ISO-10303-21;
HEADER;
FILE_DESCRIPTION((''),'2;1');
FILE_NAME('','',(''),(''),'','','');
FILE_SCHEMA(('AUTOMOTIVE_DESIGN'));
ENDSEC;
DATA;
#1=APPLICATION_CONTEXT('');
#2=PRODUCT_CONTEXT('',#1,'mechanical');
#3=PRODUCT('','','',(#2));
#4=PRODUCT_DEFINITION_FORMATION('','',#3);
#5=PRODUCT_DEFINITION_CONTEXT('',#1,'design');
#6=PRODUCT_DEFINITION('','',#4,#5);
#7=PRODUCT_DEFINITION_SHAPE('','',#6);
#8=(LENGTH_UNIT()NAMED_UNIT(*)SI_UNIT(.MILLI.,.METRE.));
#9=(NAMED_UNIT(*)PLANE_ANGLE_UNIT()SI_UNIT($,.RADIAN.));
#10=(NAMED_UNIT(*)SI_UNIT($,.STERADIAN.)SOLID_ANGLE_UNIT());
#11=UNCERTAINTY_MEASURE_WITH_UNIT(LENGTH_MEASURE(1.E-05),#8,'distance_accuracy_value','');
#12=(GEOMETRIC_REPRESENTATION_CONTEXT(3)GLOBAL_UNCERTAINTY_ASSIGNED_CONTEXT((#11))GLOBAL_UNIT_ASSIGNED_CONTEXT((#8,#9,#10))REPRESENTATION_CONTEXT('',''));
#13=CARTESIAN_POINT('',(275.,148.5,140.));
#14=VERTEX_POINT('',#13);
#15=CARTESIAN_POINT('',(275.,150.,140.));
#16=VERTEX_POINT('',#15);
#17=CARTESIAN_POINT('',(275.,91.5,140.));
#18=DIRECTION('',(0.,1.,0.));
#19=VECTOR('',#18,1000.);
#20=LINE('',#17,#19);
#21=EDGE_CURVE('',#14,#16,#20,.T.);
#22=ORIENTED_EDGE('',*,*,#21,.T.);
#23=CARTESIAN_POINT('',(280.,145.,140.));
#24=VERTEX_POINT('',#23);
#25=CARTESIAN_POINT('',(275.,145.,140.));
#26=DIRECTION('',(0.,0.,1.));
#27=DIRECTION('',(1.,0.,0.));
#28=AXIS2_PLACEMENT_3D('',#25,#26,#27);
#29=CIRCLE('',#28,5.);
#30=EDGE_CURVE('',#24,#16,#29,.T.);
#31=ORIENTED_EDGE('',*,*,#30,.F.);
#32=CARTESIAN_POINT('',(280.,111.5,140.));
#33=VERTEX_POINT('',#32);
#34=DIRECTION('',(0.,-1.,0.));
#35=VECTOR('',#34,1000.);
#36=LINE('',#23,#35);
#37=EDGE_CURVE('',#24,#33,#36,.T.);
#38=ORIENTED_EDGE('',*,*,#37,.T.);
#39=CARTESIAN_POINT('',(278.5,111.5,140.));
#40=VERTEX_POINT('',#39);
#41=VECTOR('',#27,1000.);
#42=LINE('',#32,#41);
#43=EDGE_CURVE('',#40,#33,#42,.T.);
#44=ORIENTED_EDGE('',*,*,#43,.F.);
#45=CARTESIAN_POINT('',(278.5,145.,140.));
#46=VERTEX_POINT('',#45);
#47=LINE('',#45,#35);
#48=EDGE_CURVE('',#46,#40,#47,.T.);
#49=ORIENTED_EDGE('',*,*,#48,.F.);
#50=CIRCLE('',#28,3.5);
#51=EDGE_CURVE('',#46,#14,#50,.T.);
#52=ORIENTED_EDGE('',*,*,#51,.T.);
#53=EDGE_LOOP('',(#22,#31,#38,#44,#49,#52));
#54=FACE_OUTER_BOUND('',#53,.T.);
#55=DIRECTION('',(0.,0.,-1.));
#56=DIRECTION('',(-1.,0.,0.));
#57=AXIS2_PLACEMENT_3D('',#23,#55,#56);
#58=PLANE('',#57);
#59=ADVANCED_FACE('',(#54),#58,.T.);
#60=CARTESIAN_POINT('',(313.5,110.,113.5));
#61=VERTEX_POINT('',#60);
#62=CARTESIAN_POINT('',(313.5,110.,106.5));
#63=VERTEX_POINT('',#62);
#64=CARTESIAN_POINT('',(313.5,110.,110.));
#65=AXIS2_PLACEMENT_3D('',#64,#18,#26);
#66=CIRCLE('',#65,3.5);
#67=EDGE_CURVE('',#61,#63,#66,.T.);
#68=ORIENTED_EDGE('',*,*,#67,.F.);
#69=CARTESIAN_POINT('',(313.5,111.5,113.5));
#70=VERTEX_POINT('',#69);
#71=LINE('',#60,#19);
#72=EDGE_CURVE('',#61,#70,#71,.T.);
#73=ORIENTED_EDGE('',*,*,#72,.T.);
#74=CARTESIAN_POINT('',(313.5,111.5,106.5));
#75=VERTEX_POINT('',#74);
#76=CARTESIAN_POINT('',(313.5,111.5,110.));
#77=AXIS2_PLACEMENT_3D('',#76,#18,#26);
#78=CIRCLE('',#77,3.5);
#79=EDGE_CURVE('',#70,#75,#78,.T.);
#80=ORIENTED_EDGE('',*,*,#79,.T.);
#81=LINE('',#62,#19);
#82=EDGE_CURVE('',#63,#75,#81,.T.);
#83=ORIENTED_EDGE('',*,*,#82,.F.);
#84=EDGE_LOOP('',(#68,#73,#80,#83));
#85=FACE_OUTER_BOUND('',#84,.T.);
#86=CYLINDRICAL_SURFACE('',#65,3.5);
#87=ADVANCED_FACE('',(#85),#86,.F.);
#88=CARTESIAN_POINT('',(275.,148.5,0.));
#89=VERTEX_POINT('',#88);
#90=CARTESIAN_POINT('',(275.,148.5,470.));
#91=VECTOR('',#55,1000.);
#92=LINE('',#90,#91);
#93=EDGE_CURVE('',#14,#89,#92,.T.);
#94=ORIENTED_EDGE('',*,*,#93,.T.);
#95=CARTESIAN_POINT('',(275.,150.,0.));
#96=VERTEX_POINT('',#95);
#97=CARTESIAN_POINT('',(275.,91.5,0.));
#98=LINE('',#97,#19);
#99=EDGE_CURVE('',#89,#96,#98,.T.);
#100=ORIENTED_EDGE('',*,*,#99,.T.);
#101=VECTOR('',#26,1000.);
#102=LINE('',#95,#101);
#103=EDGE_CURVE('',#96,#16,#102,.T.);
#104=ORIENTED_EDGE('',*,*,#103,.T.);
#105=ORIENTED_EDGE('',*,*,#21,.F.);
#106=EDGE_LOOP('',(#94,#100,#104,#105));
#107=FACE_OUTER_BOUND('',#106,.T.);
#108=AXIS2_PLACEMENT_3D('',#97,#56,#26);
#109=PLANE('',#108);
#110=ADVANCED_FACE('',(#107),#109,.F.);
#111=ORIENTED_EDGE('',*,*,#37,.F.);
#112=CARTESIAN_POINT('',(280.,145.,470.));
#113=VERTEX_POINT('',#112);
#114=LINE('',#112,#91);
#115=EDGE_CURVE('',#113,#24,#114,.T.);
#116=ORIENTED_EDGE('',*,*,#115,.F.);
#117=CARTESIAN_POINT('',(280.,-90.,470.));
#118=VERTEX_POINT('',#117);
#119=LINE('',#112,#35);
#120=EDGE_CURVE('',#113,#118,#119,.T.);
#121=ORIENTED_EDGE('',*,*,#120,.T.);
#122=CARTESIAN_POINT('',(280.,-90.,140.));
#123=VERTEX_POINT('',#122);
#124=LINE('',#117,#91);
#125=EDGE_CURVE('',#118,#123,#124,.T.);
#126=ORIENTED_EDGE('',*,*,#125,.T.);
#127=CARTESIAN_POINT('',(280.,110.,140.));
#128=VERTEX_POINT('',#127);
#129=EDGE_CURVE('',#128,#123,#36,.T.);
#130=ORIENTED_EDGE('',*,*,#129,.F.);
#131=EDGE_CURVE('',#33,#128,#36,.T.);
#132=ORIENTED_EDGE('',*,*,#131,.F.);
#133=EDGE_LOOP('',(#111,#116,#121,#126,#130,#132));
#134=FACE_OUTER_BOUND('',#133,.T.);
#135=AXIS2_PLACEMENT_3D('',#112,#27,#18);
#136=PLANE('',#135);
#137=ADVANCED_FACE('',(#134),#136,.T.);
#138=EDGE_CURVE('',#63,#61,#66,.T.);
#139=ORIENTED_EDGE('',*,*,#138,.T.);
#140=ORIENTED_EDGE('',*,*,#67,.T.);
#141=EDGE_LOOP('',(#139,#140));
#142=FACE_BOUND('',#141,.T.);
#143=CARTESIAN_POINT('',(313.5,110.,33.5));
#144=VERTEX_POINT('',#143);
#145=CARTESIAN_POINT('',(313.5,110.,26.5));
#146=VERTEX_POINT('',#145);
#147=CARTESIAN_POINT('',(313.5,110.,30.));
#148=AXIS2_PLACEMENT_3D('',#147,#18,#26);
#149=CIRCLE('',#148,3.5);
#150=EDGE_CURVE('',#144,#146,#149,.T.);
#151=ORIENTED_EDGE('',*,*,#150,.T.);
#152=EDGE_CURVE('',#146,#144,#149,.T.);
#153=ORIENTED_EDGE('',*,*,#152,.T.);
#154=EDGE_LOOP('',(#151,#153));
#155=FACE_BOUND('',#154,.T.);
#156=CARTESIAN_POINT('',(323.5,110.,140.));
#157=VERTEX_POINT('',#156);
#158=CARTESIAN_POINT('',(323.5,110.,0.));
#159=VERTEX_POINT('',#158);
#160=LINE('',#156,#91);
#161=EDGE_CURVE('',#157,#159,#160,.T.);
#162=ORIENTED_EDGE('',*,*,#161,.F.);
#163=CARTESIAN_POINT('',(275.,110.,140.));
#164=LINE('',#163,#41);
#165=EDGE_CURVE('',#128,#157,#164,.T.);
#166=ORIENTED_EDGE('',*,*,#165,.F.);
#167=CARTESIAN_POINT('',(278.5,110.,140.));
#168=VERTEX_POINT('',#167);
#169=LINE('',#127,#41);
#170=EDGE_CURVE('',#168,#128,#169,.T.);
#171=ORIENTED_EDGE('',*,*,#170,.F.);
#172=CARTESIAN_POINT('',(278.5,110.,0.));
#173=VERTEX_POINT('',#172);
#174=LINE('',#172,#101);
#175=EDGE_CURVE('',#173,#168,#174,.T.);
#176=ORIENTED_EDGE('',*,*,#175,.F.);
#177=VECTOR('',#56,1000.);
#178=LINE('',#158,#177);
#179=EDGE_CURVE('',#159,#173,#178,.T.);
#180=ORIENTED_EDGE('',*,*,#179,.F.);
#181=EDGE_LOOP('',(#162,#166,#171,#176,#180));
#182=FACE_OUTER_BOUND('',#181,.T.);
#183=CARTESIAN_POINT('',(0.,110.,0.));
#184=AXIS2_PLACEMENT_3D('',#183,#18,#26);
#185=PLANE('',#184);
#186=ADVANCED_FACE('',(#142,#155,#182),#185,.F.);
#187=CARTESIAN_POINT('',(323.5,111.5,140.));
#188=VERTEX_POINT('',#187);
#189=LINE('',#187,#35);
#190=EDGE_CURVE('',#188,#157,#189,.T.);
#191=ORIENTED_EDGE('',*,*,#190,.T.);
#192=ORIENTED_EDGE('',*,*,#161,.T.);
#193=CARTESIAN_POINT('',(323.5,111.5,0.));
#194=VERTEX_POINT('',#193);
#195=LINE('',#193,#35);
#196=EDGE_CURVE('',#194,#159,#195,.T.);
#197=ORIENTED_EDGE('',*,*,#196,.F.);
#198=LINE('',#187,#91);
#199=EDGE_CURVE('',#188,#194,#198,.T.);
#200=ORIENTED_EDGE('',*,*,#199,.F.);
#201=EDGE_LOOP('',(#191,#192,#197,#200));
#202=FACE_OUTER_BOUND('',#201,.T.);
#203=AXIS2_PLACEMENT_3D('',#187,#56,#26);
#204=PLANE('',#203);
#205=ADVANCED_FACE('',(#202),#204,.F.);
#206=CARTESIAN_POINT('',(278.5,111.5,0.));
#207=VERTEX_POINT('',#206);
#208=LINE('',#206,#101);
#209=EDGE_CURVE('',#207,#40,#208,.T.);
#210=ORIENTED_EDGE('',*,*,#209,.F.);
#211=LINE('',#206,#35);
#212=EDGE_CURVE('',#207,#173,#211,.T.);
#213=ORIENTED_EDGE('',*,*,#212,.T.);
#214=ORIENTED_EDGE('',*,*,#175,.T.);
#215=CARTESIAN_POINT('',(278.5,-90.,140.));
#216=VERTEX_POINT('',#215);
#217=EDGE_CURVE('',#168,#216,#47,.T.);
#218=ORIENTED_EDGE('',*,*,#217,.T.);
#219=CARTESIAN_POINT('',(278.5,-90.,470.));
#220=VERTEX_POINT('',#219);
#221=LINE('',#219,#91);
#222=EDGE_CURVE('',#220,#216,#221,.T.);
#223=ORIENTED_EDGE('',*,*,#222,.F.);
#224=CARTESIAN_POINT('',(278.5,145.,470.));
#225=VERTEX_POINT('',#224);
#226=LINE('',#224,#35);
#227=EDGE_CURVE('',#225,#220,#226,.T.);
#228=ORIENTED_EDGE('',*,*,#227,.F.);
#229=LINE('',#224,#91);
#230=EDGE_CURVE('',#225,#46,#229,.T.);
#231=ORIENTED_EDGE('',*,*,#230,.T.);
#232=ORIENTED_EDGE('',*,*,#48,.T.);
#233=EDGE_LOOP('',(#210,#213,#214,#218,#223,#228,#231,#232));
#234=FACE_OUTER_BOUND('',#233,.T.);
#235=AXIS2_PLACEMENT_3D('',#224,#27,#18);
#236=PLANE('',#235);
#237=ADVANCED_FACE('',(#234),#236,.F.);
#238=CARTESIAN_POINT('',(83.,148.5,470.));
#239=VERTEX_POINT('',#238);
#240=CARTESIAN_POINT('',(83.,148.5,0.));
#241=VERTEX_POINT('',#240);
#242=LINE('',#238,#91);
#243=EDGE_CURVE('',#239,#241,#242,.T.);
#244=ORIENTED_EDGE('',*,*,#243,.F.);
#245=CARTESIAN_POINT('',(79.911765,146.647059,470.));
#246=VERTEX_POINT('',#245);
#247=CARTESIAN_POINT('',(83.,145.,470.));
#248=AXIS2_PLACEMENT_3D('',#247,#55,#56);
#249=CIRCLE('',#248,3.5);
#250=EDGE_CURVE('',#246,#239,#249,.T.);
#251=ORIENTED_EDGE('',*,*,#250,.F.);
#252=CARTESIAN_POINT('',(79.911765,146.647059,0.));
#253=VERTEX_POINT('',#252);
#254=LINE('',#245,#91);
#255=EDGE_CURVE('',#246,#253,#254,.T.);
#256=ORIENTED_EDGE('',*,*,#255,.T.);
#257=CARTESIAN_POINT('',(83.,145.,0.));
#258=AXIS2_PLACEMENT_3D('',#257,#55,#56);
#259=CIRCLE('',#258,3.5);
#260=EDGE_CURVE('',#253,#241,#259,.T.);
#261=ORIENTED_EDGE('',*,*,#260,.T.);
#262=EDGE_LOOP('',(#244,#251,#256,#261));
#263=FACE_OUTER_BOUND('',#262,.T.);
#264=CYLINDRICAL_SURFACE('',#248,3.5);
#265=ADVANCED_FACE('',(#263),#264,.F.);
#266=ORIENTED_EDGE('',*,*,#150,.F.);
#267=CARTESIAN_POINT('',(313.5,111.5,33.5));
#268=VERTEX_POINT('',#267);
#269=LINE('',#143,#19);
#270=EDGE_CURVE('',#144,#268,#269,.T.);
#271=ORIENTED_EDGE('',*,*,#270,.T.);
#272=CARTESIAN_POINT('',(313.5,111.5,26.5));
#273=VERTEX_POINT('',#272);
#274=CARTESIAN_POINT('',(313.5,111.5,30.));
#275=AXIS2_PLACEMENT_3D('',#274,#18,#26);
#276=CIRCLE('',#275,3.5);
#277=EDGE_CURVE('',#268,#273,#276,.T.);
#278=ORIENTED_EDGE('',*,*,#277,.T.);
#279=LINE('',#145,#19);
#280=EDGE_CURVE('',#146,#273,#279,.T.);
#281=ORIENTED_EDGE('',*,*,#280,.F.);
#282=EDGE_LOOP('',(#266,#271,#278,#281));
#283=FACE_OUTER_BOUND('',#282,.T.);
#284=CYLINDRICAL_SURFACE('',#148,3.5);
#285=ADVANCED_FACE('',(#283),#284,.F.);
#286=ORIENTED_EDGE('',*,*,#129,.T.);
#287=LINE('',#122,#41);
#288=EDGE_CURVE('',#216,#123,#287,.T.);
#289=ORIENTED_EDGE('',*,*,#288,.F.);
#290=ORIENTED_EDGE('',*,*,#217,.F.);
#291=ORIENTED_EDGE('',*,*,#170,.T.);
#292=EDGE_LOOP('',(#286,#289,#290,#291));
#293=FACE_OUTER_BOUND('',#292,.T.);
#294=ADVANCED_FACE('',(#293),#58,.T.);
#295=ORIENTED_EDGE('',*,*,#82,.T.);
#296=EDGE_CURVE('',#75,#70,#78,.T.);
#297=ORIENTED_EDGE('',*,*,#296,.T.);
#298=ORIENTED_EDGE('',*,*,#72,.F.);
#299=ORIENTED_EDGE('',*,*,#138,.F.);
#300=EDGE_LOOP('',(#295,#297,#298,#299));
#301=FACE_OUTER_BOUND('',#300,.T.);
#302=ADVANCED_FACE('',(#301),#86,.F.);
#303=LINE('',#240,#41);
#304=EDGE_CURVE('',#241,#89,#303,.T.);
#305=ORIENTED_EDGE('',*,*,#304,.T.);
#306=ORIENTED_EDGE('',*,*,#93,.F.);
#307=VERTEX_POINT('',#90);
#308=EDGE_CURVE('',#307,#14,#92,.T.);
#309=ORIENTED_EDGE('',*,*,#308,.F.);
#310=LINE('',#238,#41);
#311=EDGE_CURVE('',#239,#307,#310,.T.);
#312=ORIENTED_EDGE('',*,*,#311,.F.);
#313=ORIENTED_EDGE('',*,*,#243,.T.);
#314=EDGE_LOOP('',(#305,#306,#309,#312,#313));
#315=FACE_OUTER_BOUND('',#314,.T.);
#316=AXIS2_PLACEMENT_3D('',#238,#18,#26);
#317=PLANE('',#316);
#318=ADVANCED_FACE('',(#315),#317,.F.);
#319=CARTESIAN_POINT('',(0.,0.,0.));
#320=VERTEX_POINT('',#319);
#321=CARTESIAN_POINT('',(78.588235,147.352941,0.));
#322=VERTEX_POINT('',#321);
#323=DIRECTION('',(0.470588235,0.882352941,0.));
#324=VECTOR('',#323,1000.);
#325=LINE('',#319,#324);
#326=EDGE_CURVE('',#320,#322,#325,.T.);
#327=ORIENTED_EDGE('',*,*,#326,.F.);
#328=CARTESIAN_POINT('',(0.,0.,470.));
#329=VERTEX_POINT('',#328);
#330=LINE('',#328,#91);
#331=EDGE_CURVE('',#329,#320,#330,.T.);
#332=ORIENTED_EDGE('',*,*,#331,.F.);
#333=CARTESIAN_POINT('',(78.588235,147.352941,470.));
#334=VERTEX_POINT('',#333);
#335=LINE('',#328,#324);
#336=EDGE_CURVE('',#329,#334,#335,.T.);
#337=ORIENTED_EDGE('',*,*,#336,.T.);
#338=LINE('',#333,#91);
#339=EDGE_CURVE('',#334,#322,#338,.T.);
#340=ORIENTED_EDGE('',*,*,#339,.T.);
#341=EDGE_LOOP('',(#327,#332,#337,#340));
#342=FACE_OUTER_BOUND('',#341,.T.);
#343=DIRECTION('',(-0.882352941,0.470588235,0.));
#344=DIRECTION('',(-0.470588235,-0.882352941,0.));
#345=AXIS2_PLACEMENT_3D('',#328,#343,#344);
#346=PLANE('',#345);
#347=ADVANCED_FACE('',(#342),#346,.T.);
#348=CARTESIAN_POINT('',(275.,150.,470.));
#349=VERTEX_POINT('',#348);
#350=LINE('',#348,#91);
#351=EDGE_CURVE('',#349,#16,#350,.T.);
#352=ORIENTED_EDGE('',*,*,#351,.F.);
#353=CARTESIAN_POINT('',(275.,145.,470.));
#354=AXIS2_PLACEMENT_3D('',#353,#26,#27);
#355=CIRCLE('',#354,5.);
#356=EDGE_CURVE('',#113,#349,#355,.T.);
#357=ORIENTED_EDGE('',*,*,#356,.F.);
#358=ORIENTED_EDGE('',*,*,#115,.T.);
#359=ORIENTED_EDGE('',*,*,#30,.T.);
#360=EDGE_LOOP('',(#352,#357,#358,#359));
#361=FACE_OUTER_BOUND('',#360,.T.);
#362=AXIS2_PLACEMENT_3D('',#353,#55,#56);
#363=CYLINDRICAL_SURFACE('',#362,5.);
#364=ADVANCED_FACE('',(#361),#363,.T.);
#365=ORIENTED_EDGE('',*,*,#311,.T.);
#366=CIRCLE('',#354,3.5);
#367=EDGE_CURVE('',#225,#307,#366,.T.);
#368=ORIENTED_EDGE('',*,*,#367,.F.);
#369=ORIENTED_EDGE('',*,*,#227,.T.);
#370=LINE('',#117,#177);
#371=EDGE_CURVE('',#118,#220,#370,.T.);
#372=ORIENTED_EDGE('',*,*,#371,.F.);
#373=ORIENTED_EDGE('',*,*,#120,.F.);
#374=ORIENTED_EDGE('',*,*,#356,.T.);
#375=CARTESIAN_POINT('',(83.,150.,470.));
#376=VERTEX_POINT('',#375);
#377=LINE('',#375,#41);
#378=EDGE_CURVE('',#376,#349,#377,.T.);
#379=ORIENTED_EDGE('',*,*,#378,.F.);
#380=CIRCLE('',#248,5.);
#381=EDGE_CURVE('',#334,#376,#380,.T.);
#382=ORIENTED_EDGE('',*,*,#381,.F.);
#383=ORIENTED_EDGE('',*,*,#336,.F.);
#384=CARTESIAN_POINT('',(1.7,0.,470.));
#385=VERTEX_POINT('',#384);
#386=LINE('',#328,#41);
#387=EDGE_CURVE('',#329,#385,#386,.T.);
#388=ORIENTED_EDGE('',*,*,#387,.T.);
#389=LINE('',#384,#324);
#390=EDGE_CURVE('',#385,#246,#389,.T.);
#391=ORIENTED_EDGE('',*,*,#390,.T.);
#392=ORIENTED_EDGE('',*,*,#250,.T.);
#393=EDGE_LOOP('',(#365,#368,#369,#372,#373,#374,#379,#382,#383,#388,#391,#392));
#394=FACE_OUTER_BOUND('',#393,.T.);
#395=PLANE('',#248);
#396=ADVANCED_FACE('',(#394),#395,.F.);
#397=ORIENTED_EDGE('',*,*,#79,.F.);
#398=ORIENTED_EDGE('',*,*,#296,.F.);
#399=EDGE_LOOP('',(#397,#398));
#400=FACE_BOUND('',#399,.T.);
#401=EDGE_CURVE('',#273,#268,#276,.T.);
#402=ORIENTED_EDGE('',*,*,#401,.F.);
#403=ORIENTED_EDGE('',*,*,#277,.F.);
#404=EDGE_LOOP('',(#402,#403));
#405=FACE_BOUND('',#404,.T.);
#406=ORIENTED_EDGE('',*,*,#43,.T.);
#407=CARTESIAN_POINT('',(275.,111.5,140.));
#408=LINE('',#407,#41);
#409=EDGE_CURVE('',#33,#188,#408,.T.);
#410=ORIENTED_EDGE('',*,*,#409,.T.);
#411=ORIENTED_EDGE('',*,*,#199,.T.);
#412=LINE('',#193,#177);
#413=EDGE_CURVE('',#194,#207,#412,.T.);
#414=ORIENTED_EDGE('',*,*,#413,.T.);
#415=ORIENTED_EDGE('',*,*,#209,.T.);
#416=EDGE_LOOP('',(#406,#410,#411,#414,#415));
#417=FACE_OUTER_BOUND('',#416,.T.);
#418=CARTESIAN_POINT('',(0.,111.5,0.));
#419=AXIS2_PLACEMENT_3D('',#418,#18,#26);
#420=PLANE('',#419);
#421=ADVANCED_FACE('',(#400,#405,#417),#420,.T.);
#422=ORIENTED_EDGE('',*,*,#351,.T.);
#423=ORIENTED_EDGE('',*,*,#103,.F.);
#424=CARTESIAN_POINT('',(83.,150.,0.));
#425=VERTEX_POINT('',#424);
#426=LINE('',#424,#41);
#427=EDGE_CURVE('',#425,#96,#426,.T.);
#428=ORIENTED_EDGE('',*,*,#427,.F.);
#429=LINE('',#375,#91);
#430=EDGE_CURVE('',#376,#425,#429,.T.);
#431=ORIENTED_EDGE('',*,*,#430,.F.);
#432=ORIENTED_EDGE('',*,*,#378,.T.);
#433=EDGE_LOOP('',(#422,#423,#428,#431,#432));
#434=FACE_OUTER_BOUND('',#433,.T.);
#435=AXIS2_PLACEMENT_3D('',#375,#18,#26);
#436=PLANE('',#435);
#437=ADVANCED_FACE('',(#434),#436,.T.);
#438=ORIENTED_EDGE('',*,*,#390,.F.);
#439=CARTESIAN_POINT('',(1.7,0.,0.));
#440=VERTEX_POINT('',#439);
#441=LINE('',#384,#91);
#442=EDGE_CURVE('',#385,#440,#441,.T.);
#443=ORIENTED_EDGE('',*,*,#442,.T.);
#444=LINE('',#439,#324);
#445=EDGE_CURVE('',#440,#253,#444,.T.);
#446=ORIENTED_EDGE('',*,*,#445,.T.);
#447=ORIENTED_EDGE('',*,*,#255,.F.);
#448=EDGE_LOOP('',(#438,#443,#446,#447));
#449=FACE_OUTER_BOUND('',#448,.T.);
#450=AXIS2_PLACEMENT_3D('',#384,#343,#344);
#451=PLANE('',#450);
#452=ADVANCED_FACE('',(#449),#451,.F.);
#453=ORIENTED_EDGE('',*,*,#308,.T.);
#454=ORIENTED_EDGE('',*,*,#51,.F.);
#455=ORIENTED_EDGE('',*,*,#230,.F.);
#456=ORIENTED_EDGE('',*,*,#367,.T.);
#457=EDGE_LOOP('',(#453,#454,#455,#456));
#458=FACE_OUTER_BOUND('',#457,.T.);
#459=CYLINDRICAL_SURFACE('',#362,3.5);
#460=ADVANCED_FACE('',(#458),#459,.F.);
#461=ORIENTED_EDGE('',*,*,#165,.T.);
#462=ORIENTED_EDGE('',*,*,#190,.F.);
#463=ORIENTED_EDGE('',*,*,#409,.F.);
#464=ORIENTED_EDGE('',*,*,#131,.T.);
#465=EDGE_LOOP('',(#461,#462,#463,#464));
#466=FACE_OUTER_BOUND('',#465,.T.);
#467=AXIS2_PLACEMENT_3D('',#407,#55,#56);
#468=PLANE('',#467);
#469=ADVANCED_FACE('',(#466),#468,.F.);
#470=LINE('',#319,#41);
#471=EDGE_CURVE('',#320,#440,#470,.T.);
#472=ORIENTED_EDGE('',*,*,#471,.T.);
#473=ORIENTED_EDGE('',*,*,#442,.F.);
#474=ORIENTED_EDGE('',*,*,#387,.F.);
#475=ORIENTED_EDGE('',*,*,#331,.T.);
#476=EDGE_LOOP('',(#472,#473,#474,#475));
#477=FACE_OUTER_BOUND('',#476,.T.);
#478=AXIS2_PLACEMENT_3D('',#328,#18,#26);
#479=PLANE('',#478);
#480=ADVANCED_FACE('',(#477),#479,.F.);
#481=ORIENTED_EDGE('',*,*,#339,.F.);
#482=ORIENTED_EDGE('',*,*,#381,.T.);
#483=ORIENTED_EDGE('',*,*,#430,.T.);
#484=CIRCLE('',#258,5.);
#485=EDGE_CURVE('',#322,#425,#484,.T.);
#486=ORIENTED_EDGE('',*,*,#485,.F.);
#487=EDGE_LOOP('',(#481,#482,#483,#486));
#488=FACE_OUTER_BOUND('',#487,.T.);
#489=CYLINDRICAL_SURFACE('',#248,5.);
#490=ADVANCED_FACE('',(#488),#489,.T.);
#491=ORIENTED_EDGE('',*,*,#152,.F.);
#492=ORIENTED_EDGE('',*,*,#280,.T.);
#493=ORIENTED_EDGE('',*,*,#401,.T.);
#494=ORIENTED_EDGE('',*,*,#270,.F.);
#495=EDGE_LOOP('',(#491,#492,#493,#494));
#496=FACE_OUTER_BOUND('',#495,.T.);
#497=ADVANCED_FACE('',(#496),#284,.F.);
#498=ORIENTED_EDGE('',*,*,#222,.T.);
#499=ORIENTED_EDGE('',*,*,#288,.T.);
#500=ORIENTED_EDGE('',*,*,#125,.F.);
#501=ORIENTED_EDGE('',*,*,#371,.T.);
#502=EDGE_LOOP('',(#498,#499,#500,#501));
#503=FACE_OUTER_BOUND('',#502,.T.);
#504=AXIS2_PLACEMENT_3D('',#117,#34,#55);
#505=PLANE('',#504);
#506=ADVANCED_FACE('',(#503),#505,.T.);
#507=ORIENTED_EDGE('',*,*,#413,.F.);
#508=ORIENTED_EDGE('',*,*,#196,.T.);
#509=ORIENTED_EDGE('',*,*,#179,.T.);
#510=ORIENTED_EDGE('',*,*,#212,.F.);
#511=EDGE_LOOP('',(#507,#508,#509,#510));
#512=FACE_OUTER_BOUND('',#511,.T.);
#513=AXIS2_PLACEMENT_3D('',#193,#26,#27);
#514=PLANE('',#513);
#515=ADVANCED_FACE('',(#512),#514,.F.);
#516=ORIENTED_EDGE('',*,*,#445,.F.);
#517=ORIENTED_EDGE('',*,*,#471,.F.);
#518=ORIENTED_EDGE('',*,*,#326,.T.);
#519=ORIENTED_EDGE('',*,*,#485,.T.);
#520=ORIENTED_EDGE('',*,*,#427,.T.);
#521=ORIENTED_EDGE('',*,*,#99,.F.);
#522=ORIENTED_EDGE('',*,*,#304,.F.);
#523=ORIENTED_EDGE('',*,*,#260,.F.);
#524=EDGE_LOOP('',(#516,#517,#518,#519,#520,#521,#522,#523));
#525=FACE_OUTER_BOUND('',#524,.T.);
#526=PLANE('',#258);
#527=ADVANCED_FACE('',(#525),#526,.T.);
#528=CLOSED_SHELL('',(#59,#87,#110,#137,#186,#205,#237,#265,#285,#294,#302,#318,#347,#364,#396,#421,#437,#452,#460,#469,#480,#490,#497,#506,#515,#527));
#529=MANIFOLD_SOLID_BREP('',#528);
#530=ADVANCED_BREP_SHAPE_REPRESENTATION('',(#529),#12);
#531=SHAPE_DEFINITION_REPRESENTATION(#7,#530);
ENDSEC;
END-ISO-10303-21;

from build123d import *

# Parameters (mm, degrees)
BOSS_EXTRUDE1_DEPTH = 470
SKETCH2_W           = 259.384711363
SKETCH2_H           = 314.468537248
CUT_EXTRUDE3_DEPTH  = 1.5
SKETCH5_W           = 57.928223487
SKETCH5_H           = 140
CUT_EXTRUDE9_DEPTH  = 58.5
SKETCH7_W           = 48.5
SKETCH7_H           = 140
BOSS_EXTRUDE3_DEPTH = 1.5
MOVE_FACE1_BY       = 3.5
SKETCH9_R           = 3.5
CUT_EXTRUDE10_DEPTH = 1.5


with BuildPart() as part:
    # Sketch1 → Boss-Extrude1 (new body)
    with BuildSketch(Plane.XY):
        with BuildLine():
            Line((0, 0), (78.588235294, 147.352941176))
            ThreePointArc((78.588235294, 147.352941176), (80.427521223, 149.287464629), (83, 150))
            Line((83, 150), (275, 150))
            ThreePointArc((275, 150), (278.535533906, 148.535533906), (280, 145))
            Line((280, 145), (280, -90))
            Line((280, -90), (278.5, -90))
            Line((278.5, -90), (278.5, 145))
            ThreePointArc((278.5, 145), (277.474873734, 147.474873734), (275, 148.5))
            Line((275, 148.5), (83, 148.5))
            ThreePointArc((83, 148.5), (81.199264856, 148.00122524), (79.911764706, 146.647058824))
            Line((79.911764706, 146.647058824), (1.7, 0))
            Line((1.7, 0), (0, 0))
        make_face()
    extrude(amount=BOSS_EXTRUDE1_DEPTH)

    # Sketch2 → Cut-Extrude3 (cut)
    with BuildSketch(Plane.ZY.offset(-278.5)):
        with Locations((10.307644318, -12.234268624)):
            Rectangle(SKETCH2_W, SKETCH2_H)
    extrude(amount=-CUT_EXTRUDE3_DEPTH, mode=Mode.SUBTRACT)

    # Sketch5 → Cut-Extrude9 (cut)
    with BuildSketch(Plane(origin=(0, 150, 0), x_dir=(1, 0, 0), z_dir=(0, 1, 0))):
        with Locations((303.964111743, -70)):
            Rectangle(SKETCH5_W, SKETCH5_H)
    extrude(amount=-CUT_EXTRUDE9_DEPTH, mode=Mode.SUBTRACT)

    # Sketch7 → Boss-Extrude3 (add)
    with BuildSketch(Plane(origin=(0, 110, 0), x_dir=(1, 0, 0), z_dir=(0, 1, 0))):
        with Locations((299.25, -70)):
            Rectangle(SKETCH7_W, SKETCH7_H)
    extrude(amount=BOSS_EXTRUDE3_DEPTH)

    # Move Face1: a face moved inward by 3.5
    extrude(part.faces().sort_by_distance((275, 110.75, 70))[0], amount=MOVE_FACE1_BY, dir=(1, 0, 0), mode=Mode.SUBTRACT)

    # Sketch9 → Cut-Extrude10 (cut)
    with BuildSketch(Plane(origin=(0, 111.5, 0), x_dir=(1, 0, 0), z_dir=(0, 1, 0))):
        with Locations(Location((313.5, -30, 0), (0, 0, 270))):
            Circle(SKETCH9_R)
        with Locations(Location((313.5, -110, 0), (0, 0, 270))):
            Circle(SKETCH9_R)
    extrude(amount=-CUT_EXTRUDE10_DEPTH, mode=Mode.SUBTRACT)


solid = part.part
